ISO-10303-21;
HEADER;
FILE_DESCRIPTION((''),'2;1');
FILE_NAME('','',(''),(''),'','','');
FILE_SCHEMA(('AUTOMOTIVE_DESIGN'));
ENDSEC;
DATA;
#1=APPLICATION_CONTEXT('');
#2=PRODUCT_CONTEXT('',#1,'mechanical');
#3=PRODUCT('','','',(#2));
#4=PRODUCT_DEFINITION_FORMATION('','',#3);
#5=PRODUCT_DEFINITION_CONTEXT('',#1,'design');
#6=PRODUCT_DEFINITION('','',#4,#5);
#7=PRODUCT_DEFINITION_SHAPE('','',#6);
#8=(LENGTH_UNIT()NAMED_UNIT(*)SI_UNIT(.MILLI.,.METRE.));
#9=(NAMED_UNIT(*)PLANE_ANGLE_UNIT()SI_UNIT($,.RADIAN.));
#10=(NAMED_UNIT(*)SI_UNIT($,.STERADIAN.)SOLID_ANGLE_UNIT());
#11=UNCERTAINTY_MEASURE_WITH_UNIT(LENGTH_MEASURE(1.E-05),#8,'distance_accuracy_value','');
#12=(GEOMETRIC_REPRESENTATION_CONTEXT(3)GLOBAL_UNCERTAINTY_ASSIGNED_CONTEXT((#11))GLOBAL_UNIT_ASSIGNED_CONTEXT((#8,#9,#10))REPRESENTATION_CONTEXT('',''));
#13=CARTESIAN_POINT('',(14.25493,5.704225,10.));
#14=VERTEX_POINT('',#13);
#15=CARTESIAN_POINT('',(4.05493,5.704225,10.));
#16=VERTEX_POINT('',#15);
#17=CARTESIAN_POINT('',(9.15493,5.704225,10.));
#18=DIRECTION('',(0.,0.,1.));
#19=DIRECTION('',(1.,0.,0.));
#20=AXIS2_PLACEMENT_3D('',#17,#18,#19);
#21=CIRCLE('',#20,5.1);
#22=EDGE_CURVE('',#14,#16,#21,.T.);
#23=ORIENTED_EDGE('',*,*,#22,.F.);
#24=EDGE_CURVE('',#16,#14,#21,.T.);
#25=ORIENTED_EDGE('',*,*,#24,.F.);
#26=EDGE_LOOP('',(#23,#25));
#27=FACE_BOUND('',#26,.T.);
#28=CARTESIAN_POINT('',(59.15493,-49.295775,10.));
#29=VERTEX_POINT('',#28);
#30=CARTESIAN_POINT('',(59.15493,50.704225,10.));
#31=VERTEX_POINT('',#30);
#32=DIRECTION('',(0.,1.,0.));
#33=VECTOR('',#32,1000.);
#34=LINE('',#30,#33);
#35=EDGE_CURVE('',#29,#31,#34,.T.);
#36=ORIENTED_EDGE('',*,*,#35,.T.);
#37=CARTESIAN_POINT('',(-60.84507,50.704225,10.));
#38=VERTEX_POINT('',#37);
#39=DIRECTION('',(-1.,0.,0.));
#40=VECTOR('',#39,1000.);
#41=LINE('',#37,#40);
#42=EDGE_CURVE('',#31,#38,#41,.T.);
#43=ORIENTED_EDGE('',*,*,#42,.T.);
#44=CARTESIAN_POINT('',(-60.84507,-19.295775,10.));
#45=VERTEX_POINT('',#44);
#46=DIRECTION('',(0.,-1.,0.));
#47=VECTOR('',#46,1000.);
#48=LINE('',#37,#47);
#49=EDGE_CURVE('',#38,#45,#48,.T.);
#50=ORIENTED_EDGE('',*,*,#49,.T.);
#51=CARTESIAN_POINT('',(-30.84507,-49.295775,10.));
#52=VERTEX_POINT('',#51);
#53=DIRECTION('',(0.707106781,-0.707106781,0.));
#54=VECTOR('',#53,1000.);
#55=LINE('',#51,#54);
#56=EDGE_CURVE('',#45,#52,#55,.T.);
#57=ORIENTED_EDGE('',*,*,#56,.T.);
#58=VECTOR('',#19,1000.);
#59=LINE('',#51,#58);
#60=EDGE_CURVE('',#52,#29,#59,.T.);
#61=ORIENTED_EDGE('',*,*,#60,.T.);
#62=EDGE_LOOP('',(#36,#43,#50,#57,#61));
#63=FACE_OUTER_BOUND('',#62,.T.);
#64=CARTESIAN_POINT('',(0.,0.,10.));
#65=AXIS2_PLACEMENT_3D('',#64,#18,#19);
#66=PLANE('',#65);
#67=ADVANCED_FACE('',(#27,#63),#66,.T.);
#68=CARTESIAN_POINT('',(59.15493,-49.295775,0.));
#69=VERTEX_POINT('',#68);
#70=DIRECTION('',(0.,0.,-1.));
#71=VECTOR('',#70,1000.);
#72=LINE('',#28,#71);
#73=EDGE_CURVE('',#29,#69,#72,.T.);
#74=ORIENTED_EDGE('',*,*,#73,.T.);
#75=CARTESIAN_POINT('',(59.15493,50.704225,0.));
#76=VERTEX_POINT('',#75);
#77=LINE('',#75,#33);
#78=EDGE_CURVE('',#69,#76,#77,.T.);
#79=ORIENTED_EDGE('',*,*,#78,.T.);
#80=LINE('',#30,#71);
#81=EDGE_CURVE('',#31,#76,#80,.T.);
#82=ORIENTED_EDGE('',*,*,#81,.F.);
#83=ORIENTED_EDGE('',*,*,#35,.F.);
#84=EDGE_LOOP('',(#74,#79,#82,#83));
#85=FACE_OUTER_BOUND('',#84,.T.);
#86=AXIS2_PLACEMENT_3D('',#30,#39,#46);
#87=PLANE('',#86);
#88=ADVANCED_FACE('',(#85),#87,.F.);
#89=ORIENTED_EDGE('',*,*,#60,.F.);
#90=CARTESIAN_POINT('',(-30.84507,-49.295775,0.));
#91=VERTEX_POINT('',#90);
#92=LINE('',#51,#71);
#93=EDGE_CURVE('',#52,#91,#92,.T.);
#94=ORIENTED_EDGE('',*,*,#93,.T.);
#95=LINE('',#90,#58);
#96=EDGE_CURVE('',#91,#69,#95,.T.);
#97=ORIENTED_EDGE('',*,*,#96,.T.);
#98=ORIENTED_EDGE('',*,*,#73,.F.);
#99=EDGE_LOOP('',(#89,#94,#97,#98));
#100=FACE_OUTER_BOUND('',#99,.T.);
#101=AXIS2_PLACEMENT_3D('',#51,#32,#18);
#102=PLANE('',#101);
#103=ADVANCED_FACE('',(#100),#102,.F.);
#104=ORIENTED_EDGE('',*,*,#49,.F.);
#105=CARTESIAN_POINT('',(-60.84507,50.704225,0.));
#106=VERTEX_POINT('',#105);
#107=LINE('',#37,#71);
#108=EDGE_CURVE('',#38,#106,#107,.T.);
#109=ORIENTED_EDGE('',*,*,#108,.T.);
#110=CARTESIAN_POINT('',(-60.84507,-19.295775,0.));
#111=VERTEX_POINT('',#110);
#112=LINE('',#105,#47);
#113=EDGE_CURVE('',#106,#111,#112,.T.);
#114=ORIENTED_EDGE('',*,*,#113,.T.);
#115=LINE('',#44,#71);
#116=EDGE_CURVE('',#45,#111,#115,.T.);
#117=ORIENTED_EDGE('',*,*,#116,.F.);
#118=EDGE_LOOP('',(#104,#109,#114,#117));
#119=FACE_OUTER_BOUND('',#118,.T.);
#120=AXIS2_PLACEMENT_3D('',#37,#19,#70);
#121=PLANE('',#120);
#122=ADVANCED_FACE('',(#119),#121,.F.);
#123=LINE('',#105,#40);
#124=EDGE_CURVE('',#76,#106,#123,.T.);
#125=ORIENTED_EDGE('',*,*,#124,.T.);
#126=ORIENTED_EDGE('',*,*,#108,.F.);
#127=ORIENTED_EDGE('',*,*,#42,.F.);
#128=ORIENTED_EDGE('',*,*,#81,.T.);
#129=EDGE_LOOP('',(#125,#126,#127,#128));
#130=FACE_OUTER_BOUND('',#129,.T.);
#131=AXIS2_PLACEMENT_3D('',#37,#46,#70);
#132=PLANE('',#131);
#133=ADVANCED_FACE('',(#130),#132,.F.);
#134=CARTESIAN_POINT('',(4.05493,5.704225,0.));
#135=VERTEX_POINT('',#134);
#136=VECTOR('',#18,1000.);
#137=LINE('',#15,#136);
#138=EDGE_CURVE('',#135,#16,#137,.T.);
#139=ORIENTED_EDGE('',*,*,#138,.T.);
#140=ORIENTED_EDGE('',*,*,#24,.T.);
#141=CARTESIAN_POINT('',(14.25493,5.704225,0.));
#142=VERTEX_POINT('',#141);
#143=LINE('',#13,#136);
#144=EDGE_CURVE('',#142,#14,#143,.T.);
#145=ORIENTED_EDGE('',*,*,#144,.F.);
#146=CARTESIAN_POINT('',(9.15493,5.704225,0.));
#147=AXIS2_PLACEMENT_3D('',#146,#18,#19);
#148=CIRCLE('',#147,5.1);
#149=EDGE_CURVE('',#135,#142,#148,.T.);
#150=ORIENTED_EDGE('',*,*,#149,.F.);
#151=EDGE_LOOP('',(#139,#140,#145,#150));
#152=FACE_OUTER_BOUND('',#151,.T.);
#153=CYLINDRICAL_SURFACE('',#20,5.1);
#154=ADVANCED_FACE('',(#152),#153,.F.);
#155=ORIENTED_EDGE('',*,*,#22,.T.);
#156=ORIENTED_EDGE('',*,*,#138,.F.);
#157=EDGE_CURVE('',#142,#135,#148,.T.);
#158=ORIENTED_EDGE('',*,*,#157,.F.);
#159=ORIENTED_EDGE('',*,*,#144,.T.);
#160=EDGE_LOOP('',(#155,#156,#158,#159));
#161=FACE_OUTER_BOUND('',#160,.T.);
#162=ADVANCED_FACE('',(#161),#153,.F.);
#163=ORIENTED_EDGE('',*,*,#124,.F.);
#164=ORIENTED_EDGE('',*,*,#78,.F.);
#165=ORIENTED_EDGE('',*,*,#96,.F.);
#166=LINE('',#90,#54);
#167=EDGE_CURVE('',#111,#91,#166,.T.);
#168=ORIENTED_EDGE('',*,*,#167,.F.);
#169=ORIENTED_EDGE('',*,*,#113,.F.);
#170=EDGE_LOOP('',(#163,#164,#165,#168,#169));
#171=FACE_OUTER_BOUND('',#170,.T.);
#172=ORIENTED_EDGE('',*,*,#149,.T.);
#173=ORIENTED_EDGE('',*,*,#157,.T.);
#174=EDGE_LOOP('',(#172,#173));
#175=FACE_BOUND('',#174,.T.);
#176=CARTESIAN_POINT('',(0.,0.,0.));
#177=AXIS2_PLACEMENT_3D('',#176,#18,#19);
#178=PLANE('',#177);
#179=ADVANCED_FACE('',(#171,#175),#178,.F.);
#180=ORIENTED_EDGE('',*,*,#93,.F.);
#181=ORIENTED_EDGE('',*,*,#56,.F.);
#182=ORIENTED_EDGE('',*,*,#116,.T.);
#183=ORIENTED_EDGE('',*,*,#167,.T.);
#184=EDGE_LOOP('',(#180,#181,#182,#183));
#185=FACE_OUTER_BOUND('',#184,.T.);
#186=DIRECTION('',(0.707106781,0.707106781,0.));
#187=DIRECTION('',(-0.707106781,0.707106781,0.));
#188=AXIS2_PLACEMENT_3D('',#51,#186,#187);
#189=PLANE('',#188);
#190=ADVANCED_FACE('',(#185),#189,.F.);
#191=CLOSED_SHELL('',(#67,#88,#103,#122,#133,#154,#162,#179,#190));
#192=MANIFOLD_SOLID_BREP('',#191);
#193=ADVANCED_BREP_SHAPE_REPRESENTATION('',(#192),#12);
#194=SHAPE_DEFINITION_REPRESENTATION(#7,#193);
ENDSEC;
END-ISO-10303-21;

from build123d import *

# Parameters (mm, degrees)
EXTRUDE_1_DEPTH         = 10
HOLE_WIZARD_M12_1_D     = 10.2
HOLE_WIZARD_M12_1_DEPTH = 32.75
HOLE_WIZARD_M12_1_TIP   = 3.064389157


with BuildPart() as part:
    # 草图1 → 凸台-拉伸1 (new body)
    with BuildSketch(Plane.XY):
        Polygon((-30.845070423, -49.295774648), (-60.845070423, -19.295774648), (-60.845070423, 50.704225352), (59.154929577, 50.704225352), (59.154929577, -49.295774648), align=None)
    extrude(amount=EXTRUDE_1_DEPTH)

    # M12 螺纹孔1
    with Locations(Plane.XY.offset(10)):
        with Locations((9.154929577, 5.704225352)):
            Hole(HOLE_WIZARD_M12_1_D / 2, depth=HOLE_WIZARD_M12_1_DEPTH)
            with Locations((0, 0, -(HOLE_WIZARD_M12_1_DEPTH + HOLE_WIZARD_M12_1_TIP / 2))):  # 118° drill point
                Cone(0, HOLE_WIZARD_M12_1_D / 2, HOLE_WIZARD_M12_1_TIP, mode=Mode.SUBTRACT)


solid = part.part
